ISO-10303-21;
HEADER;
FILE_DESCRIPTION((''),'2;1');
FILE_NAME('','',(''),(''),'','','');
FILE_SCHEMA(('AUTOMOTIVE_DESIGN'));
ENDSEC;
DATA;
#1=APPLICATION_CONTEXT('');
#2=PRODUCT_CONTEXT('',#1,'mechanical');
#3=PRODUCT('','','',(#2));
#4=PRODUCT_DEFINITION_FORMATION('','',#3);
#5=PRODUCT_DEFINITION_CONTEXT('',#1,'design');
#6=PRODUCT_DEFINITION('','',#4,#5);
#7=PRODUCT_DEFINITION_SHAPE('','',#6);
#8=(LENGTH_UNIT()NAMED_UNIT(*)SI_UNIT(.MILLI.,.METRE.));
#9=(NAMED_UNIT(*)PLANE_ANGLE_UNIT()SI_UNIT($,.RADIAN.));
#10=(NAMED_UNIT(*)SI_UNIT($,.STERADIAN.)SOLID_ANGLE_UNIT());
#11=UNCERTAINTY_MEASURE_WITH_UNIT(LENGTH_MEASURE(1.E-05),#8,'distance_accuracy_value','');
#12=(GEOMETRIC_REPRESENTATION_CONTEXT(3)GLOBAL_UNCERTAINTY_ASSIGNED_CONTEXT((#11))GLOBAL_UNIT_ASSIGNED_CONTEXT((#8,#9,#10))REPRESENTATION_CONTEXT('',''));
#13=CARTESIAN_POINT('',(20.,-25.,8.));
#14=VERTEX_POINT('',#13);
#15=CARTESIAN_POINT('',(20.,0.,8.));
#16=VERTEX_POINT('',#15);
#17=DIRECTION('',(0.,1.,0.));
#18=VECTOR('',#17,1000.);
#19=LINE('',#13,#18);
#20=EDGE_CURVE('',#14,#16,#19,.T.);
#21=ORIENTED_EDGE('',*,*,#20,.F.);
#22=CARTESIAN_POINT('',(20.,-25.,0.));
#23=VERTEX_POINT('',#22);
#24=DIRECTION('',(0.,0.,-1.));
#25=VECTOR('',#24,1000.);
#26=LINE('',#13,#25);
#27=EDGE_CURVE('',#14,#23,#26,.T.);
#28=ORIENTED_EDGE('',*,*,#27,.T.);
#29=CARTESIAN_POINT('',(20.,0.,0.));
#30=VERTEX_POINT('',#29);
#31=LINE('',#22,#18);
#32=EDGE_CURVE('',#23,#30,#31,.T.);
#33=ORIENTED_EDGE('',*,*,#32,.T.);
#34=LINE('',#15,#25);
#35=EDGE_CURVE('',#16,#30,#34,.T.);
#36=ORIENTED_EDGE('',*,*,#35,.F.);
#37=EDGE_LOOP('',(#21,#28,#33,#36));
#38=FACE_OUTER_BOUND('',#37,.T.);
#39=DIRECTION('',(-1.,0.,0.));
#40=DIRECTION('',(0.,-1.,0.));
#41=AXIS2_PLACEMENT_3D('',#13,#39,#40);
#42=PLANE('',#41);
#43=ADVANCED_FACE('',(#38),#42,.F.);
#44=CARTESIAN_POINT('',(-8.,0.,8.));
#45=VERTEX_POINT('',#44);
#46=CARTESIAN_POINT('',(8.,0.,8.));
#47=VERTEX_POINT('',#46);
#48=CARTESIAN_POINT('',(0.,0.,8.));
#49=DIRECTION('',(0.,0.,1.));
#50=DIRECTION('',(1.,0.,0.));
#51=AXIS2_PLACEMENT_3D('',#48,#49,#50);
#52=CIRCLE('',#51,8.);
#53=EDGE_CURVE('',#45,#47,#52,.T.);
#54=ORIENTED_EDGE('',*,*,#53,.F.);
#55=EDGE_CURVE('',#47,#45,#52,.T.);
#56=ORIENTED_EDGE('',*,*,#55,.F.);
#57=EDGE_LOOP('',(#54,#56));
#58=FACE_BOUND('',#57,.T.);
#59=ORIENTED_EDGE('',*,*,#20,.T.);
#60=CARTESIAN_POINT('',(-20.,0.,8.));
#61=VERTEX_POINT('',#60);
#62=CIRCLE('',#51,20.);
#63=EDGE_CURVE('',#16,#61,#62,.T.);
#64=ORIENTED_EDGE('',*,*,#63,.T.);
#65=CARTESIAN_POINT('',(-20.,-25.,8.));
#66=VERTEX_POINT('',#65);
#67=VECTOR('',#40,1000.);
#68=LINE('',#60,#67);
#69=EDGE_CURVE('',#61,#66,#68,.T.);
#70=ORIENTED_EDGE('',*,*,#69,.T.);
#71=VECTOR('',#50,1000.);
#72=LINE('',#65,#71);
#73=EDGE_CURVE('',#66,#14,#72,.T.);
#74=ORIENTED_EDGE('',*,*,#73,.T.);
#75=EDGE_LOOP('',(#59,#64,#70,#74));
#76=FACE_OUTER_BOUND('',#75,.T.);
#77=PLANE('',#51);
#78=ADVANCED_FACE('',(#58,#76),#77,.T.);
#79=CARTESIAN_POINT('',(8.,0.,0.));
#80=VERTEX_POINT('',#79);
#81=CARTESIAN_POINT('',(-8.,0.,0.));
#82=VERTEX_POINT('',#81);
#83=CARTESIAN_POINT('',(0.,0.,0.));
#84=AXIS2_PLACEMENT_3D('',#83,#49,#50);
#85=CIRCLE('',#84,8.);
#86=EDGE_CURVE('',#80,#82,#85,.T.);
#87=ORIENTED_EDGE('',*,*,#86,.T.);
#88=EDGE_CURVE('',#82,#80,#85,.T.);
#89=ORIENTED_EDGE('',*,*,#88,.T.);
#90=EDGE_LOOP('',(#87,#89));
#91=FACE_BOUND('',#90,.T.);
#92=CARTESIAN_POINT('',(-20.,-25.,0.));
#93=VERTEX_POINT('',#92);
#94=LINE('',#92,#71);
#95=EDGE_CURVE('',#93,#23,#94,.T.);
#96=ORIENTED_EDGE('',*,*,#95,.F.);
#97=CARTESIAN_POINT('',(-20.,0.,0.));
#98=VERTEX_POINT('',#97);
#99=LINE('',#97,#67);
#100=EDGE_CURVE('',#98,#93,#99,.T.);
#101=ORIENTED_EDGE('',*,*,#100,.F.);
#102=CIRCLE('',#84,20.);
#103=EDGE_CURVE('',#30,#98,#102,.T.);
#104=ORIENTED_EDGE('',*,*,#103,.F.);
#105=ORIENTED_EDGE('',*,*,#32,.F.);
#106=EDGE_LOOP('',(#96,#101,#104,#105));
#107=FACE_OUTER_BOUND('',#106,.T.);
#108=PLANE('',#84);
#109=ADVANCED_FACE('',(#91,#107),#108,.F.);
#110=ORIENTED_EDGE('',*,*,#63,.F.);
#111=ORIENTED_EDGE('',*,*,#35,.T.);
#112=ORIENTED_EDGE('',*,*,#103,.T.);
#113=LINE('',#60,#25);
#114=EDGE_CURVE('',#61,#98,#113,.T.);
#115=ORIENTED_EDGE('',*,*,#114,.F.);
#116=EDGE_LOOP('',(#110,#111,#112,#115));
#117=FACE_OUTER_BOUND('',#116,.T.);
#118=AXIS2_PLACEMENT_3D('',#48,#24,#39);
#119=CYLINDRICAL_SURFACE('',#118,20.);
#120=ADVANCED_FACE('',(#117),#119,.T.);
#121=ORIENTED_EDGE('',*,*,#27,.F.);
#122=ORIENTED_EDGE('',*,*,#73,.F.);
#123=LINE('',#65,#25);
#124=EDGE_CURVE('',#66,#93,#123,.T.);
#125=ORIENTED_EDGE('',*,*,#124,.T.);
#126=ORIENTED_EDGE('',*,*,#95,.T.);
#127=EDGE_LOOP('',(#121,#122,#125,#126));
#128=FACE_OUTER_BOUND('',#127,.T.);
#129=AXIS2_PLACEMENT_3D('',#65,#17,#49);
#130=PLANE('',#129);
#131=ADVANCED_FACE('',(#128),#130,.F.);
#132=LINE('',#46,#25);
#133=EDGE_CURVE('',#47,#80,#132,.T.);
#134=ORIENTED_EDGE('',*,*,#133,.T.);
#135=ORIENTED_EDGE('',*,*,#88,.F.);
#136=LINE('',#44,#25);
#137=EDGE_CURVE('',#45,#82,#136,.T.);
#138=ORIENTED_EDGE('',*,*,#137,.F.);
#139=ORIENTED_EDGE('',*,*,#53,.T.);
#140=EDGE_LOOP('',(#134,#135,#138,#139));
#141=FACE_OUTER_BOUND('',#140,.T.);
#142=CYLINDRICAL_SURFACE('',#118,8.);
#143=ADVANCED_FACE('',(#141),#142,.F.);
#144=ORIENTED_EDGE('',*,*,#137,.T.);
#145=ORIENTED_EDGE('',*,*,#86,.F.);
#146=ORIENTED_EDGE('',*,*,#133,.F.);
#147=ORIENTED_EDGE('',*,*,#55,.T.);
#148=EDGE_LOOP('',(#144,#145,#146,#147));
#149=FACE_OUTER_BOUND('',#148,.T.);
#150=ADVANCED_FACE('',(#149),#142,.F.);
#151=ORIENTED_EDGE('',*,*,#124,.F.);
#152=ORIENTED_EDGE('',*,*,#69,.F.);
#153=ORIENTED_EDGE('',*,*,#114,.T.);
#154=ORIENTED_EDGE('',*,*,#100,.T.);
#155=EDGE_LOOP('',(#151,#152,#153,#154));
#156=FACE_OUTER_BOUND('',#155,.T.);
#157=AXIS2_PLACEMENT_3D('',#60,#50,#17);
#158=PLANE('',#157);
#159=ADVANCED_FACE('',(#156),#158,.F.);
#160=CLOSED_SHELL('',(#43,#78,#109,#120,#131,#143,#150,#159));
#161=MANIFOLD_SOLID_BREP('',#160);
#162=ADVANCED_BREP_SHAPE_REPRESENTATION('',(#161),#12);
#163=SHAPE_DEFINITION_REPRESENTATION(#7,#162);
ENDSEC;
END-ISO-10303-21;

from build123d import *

# Parameters (mm, degrees)
SKETCH1_R           = 8
BOSS_EXTRUDE1_DEPTH = 8


with BuildPart() as part:
    # Sketch1 → Boss-Extrude1 (new body)
    with BuildSketch(Plane.XY):
        with BuildLine():
            Line((-20, 0), (-20, -25))
            Line((-20, -25), (20, -25))
            Line((20, -25), (20, 0))
            ThreePointArc((20, 0), (0, 20), (-20, 0))
        make_face()
        Circle(SKETCH1_R, mode=Mode.SUBTRACT)
    extrude(amount=BOSS_EXTRUDE1_DEPTH)


solid = part.part
